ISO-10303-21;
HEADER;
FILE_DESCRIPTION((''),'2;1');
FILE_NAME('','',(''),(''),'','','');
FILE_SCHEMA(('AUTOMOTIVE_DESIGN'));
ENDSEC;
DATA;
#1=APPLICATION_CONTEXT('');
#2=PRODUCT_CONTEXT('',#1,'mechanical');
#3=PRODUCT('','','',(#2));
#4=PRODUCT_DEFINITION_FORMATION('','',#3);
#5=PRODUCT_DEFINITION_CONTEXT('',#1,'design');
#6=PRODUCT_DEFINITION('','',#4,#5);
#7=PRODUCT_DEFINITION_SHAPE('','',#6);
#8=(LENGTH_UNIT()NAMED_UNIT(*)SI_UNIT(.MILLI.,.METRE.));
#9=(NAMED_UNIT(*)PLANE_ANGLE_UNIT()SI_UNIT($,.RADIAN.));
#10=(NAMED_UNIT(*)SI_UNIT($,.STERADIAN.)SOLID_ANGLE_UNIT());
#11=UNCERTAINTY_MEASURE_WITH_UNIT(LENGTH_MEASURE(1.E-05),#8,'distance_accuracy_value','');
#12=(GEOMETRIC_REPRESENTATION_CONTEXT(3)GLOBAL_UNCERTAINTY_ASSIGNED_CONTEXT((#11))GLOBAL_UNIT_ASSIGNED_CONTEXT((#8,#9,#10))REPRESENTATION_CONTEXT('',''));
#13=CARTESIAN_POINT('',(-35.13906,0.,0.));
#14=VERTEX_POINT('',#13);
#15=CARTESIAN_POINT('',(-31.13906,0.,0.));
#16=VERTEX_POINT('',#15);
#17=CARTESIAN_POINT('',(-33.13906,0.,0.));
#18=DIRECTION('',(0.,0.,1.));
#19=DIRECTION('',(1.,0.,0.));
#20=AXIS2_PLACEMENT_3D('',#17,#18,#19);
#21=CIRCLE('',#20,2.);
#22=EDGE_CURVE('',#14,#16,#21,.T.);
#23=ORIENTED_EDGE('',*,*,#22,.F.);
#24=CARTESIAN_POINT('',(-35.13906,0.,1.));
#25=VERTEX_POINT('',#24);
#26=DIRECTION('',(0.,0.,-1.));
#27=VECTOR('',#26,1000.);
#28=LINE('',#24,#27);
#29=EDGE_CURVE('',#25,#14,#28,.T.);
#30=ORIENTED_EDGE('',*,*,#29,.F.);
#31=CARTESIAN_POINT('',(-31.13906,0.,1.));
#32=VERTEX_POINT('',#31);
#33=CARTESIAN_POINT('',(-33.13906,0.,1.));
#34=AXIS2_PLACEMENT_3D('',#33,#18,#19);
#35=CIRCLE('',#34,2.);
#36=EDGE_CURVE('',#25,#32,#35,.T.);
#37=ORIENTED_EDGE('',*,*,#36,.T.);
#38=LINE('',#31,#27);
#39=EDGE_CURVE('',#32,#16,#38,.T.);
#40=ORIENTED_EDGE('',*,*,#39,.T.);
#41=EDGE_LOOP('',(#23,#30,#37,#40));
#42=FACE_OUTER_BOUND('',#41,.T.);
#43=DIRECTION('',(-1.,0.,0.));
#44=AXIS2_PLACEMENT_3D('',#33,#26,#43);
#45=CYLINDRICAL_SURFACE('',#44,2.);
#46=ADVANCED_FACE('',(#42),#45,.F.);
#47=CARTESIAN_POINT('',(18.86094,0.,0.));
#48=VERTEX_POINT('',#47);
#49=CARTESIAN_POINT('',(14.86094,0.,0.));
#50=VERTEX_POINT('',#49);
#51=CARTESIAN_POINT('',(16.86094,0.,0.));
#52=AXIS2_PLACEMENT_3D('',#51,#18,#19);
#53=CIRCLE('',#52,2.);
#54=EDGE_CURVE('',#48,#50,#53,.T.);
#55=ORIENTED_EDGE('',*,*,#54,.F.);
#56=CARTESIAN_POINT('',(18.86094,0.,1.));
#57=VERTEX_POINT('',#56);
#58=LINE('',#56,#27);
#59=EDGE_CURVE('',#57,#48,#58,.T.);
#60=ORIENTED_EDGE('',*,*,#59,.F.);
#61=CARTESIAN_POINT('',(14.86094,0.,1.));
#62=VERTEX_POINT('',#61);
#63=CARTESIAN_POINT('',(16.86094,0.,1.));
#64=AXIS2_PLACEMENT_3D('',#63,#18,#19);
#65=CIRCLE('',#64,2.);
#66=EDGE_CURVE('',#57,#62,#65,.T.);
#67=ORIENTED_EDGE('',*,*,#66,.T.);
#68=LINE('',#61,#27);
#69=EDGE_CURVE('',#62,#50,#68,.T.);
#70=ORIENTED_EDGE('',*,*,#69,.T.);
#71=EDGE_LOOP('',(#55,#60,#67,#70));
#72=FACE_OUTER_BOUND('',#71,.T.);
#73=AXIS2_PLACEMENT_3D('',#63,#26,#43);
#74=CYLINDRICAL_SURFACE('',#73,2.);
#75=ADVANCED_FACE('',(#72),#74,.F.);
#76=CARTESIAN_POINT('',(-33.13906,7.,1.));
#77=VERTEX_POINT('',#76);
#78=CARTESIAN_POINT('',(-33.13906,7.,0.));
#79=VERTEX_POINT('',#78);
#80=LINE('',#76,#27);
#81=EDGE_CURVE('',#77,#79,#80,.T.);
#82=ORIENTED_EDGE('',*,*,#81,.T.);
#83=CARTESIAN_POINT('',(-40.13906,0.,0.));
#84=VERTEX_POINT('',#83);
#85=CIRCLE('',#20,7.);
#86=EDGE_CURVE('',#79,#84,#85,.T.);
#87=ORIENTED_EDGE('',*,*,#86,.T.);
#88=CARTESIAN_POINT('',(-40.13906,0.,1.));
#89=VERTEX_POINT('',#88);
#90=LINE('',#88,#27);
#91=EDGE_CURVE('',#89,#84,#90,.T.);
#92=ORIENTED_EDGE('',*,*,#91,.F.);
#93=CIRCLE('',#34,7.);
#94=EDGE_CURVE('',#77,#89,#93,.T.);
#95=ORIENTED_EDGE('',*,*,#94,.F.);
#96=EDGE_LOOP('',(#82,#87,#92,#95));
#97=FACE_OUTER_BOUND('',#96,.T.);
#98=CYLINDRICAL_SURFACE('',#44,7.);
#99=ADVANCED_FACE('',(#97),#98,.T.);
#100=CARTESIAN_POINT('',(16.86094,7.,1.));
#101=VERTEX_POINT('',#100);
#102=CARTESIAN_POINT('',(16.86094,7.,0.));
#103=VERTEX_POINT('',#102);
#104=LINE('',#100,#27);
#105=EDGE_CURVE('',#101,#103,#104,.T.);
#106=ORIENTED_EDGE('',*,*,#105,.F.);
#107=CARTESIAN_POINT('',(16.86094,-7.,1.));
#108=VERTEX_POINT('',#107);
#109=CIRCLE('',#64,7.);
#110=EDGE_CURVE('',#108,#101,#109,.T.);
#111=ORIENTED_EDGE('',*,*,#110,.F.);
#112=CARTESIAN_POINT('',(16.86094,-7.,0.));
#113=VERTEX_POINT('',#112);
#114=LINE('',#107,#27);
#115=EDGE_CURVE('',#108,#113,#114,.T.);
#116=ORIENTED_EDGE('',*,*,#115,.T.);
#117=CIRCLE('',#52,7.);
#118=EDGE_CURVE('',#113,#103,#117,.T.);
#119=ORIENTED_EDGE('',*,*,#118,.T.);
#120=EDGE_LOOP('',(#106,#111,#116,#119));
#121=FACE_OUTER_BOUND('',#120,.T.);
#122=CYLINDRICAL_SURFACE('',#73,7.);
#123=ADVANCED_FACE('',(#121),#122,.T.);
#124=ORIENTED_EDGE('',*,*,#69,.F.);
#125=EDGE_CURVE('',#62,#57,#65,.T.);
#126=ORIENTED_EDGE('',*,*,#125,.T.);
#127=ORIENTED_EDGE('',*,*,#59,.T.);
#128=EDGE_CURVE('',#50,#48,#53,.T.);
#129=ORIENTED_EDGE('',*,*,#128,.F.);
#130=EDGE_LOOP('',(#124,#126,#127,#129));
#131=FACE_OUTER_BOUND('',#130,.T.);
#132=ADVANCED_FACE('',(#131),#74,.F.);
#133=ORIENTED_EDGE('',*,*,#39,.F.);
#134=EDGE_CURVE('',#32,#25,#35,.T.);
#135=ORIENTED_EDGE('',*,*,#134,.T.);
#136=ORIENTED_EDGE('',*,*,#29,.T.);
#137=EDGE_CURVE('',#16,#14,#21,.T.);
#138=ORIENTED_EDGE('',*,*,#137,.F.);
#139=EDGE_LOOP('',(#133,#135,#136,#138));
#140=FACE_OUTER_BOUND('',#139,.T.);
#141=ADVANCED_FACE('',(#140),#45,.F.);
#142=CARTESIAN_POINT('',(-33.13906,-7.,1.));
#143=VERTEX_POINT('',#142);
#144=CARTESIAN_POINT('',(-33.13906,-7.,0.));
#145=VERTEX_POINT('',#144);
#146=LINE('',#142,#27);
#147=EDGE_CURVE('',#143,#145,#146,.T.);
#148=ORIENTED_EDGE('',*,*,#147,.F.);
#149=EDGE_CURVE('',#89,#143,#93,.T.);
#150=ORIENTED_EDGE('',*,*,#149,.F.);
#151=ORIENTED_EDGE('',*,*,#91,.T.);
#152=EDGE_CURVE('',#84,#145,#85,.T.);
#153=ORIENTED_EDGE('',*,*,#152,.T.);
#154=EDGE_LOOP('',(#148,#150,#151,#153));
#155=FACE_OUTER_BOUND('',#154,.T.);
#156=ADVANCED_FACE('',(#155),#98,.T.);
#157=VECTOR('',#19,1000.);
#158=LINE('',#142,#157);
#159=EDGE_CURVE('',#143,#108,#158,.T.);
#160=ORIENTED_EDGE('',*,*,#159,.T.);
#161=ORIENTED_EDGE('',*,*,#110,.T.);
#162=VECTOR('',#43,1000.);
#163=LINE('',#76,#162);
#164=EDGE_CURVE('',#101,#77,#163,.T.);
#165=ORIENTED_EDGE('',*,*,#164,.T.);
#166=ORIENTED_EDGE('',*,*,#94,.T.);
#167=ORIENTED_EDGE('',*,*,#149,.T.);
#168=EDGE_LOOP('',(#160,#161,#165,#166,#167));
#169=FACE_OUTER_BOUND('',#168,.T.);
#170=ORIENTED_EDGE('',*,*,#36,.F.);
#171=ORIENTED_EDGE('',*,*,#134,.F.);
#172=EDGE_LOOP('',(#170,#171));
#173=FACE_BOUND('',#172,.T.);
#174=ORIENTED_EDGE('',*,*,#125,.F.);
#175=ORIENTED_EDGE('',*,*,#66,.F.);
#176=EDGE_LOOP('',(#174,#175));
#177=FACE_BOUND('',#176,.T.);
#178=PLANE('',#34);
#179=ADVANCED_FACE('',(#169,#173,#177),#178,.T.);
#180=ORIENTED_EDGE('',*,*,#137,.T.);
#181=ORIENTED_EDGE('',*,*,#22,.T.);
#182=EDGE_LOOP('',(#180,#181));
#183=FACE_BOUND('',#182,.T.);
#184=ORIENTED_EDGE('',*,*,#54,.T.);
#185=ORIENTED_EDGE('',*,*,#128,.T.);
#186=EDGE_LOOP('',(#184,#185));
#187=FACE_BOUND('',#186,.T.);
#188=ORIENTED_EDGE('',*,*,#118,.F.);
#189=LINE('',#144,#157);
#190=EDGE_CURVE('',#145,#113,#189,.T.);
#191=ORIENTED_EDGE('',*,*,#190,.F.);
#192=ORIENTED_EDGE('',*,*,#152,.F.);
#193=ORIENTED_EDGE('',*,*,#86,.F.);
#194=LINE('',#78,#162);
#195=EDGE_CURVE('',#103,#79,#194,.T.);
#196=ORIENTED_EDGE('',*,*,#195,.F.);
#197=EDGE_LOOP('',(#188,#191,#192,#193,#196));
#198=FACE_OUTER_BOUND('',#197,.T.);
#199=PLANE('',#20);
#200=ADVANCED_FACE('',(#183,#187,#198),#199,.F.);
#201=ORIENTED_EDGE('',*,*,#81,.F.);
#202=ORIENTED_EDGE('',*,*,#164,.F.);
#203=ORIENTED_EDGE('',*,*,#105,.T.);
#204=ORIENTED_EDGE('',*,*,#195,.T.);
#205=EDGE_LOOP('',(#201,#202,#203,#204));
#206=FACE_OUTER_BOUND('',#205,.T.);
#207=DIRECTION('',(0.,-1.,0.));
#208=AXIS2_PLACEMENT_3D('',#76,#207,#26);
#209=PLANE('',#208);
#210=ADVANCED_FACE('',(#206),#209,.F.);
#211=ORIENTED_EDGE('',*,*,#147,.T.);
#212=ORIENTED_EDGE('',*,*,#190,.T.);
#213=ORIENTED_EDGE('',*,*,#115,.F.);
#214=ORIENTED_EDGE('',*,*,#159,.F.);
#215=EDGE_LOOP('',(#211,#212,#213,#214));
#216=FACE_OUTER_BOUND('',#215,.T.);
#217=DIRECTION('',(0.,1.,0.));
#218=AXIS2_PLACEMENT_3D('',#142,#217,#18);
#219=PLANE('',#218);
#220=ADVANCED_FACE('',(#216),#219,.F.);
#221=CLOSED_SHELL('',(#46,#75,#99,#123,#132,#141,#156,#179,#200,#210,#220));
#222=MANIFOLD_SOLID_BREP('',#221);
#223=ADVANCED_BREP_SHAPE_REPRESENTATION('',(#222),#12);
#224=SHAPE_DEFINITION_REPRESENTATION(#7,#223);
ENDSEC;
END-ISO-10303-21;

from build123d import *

# Parameters (mm, degrees)
SKETCH1_R           = 2
BOSS_EXTRUDE1_DEPTH = 1


with BuildPart() as part:
    # Sketch1 → Boss-Extrude1 (new body)
    with BuildSketch(Plane.XY):
        with BuildLine():
            Line((-33.139059677, 7), (16.860940323, 7))
            ThreePointArc((16.860940323, 7), (23.860940323, 0), (16.860940323, -7))
            Line((16.860940323, -7), (-33.139059677, -7))
            ThreePointArc((-33.139059677, -7), (-40.139059677, 0), (-33.139059677, 7))
        make_face()
        with Locations((-33.139059677, 0)):
            Circle(SKETCH1_R, mode=Mode.SUBTRACT)
        with Locations((16.860940323, 0)):
            Circle(SKETCH1_R, mode=Mode.SUBTRACT)
    extrude(amount=BOSS_EXTRUDE1_DEPTH)


solid = part.part
